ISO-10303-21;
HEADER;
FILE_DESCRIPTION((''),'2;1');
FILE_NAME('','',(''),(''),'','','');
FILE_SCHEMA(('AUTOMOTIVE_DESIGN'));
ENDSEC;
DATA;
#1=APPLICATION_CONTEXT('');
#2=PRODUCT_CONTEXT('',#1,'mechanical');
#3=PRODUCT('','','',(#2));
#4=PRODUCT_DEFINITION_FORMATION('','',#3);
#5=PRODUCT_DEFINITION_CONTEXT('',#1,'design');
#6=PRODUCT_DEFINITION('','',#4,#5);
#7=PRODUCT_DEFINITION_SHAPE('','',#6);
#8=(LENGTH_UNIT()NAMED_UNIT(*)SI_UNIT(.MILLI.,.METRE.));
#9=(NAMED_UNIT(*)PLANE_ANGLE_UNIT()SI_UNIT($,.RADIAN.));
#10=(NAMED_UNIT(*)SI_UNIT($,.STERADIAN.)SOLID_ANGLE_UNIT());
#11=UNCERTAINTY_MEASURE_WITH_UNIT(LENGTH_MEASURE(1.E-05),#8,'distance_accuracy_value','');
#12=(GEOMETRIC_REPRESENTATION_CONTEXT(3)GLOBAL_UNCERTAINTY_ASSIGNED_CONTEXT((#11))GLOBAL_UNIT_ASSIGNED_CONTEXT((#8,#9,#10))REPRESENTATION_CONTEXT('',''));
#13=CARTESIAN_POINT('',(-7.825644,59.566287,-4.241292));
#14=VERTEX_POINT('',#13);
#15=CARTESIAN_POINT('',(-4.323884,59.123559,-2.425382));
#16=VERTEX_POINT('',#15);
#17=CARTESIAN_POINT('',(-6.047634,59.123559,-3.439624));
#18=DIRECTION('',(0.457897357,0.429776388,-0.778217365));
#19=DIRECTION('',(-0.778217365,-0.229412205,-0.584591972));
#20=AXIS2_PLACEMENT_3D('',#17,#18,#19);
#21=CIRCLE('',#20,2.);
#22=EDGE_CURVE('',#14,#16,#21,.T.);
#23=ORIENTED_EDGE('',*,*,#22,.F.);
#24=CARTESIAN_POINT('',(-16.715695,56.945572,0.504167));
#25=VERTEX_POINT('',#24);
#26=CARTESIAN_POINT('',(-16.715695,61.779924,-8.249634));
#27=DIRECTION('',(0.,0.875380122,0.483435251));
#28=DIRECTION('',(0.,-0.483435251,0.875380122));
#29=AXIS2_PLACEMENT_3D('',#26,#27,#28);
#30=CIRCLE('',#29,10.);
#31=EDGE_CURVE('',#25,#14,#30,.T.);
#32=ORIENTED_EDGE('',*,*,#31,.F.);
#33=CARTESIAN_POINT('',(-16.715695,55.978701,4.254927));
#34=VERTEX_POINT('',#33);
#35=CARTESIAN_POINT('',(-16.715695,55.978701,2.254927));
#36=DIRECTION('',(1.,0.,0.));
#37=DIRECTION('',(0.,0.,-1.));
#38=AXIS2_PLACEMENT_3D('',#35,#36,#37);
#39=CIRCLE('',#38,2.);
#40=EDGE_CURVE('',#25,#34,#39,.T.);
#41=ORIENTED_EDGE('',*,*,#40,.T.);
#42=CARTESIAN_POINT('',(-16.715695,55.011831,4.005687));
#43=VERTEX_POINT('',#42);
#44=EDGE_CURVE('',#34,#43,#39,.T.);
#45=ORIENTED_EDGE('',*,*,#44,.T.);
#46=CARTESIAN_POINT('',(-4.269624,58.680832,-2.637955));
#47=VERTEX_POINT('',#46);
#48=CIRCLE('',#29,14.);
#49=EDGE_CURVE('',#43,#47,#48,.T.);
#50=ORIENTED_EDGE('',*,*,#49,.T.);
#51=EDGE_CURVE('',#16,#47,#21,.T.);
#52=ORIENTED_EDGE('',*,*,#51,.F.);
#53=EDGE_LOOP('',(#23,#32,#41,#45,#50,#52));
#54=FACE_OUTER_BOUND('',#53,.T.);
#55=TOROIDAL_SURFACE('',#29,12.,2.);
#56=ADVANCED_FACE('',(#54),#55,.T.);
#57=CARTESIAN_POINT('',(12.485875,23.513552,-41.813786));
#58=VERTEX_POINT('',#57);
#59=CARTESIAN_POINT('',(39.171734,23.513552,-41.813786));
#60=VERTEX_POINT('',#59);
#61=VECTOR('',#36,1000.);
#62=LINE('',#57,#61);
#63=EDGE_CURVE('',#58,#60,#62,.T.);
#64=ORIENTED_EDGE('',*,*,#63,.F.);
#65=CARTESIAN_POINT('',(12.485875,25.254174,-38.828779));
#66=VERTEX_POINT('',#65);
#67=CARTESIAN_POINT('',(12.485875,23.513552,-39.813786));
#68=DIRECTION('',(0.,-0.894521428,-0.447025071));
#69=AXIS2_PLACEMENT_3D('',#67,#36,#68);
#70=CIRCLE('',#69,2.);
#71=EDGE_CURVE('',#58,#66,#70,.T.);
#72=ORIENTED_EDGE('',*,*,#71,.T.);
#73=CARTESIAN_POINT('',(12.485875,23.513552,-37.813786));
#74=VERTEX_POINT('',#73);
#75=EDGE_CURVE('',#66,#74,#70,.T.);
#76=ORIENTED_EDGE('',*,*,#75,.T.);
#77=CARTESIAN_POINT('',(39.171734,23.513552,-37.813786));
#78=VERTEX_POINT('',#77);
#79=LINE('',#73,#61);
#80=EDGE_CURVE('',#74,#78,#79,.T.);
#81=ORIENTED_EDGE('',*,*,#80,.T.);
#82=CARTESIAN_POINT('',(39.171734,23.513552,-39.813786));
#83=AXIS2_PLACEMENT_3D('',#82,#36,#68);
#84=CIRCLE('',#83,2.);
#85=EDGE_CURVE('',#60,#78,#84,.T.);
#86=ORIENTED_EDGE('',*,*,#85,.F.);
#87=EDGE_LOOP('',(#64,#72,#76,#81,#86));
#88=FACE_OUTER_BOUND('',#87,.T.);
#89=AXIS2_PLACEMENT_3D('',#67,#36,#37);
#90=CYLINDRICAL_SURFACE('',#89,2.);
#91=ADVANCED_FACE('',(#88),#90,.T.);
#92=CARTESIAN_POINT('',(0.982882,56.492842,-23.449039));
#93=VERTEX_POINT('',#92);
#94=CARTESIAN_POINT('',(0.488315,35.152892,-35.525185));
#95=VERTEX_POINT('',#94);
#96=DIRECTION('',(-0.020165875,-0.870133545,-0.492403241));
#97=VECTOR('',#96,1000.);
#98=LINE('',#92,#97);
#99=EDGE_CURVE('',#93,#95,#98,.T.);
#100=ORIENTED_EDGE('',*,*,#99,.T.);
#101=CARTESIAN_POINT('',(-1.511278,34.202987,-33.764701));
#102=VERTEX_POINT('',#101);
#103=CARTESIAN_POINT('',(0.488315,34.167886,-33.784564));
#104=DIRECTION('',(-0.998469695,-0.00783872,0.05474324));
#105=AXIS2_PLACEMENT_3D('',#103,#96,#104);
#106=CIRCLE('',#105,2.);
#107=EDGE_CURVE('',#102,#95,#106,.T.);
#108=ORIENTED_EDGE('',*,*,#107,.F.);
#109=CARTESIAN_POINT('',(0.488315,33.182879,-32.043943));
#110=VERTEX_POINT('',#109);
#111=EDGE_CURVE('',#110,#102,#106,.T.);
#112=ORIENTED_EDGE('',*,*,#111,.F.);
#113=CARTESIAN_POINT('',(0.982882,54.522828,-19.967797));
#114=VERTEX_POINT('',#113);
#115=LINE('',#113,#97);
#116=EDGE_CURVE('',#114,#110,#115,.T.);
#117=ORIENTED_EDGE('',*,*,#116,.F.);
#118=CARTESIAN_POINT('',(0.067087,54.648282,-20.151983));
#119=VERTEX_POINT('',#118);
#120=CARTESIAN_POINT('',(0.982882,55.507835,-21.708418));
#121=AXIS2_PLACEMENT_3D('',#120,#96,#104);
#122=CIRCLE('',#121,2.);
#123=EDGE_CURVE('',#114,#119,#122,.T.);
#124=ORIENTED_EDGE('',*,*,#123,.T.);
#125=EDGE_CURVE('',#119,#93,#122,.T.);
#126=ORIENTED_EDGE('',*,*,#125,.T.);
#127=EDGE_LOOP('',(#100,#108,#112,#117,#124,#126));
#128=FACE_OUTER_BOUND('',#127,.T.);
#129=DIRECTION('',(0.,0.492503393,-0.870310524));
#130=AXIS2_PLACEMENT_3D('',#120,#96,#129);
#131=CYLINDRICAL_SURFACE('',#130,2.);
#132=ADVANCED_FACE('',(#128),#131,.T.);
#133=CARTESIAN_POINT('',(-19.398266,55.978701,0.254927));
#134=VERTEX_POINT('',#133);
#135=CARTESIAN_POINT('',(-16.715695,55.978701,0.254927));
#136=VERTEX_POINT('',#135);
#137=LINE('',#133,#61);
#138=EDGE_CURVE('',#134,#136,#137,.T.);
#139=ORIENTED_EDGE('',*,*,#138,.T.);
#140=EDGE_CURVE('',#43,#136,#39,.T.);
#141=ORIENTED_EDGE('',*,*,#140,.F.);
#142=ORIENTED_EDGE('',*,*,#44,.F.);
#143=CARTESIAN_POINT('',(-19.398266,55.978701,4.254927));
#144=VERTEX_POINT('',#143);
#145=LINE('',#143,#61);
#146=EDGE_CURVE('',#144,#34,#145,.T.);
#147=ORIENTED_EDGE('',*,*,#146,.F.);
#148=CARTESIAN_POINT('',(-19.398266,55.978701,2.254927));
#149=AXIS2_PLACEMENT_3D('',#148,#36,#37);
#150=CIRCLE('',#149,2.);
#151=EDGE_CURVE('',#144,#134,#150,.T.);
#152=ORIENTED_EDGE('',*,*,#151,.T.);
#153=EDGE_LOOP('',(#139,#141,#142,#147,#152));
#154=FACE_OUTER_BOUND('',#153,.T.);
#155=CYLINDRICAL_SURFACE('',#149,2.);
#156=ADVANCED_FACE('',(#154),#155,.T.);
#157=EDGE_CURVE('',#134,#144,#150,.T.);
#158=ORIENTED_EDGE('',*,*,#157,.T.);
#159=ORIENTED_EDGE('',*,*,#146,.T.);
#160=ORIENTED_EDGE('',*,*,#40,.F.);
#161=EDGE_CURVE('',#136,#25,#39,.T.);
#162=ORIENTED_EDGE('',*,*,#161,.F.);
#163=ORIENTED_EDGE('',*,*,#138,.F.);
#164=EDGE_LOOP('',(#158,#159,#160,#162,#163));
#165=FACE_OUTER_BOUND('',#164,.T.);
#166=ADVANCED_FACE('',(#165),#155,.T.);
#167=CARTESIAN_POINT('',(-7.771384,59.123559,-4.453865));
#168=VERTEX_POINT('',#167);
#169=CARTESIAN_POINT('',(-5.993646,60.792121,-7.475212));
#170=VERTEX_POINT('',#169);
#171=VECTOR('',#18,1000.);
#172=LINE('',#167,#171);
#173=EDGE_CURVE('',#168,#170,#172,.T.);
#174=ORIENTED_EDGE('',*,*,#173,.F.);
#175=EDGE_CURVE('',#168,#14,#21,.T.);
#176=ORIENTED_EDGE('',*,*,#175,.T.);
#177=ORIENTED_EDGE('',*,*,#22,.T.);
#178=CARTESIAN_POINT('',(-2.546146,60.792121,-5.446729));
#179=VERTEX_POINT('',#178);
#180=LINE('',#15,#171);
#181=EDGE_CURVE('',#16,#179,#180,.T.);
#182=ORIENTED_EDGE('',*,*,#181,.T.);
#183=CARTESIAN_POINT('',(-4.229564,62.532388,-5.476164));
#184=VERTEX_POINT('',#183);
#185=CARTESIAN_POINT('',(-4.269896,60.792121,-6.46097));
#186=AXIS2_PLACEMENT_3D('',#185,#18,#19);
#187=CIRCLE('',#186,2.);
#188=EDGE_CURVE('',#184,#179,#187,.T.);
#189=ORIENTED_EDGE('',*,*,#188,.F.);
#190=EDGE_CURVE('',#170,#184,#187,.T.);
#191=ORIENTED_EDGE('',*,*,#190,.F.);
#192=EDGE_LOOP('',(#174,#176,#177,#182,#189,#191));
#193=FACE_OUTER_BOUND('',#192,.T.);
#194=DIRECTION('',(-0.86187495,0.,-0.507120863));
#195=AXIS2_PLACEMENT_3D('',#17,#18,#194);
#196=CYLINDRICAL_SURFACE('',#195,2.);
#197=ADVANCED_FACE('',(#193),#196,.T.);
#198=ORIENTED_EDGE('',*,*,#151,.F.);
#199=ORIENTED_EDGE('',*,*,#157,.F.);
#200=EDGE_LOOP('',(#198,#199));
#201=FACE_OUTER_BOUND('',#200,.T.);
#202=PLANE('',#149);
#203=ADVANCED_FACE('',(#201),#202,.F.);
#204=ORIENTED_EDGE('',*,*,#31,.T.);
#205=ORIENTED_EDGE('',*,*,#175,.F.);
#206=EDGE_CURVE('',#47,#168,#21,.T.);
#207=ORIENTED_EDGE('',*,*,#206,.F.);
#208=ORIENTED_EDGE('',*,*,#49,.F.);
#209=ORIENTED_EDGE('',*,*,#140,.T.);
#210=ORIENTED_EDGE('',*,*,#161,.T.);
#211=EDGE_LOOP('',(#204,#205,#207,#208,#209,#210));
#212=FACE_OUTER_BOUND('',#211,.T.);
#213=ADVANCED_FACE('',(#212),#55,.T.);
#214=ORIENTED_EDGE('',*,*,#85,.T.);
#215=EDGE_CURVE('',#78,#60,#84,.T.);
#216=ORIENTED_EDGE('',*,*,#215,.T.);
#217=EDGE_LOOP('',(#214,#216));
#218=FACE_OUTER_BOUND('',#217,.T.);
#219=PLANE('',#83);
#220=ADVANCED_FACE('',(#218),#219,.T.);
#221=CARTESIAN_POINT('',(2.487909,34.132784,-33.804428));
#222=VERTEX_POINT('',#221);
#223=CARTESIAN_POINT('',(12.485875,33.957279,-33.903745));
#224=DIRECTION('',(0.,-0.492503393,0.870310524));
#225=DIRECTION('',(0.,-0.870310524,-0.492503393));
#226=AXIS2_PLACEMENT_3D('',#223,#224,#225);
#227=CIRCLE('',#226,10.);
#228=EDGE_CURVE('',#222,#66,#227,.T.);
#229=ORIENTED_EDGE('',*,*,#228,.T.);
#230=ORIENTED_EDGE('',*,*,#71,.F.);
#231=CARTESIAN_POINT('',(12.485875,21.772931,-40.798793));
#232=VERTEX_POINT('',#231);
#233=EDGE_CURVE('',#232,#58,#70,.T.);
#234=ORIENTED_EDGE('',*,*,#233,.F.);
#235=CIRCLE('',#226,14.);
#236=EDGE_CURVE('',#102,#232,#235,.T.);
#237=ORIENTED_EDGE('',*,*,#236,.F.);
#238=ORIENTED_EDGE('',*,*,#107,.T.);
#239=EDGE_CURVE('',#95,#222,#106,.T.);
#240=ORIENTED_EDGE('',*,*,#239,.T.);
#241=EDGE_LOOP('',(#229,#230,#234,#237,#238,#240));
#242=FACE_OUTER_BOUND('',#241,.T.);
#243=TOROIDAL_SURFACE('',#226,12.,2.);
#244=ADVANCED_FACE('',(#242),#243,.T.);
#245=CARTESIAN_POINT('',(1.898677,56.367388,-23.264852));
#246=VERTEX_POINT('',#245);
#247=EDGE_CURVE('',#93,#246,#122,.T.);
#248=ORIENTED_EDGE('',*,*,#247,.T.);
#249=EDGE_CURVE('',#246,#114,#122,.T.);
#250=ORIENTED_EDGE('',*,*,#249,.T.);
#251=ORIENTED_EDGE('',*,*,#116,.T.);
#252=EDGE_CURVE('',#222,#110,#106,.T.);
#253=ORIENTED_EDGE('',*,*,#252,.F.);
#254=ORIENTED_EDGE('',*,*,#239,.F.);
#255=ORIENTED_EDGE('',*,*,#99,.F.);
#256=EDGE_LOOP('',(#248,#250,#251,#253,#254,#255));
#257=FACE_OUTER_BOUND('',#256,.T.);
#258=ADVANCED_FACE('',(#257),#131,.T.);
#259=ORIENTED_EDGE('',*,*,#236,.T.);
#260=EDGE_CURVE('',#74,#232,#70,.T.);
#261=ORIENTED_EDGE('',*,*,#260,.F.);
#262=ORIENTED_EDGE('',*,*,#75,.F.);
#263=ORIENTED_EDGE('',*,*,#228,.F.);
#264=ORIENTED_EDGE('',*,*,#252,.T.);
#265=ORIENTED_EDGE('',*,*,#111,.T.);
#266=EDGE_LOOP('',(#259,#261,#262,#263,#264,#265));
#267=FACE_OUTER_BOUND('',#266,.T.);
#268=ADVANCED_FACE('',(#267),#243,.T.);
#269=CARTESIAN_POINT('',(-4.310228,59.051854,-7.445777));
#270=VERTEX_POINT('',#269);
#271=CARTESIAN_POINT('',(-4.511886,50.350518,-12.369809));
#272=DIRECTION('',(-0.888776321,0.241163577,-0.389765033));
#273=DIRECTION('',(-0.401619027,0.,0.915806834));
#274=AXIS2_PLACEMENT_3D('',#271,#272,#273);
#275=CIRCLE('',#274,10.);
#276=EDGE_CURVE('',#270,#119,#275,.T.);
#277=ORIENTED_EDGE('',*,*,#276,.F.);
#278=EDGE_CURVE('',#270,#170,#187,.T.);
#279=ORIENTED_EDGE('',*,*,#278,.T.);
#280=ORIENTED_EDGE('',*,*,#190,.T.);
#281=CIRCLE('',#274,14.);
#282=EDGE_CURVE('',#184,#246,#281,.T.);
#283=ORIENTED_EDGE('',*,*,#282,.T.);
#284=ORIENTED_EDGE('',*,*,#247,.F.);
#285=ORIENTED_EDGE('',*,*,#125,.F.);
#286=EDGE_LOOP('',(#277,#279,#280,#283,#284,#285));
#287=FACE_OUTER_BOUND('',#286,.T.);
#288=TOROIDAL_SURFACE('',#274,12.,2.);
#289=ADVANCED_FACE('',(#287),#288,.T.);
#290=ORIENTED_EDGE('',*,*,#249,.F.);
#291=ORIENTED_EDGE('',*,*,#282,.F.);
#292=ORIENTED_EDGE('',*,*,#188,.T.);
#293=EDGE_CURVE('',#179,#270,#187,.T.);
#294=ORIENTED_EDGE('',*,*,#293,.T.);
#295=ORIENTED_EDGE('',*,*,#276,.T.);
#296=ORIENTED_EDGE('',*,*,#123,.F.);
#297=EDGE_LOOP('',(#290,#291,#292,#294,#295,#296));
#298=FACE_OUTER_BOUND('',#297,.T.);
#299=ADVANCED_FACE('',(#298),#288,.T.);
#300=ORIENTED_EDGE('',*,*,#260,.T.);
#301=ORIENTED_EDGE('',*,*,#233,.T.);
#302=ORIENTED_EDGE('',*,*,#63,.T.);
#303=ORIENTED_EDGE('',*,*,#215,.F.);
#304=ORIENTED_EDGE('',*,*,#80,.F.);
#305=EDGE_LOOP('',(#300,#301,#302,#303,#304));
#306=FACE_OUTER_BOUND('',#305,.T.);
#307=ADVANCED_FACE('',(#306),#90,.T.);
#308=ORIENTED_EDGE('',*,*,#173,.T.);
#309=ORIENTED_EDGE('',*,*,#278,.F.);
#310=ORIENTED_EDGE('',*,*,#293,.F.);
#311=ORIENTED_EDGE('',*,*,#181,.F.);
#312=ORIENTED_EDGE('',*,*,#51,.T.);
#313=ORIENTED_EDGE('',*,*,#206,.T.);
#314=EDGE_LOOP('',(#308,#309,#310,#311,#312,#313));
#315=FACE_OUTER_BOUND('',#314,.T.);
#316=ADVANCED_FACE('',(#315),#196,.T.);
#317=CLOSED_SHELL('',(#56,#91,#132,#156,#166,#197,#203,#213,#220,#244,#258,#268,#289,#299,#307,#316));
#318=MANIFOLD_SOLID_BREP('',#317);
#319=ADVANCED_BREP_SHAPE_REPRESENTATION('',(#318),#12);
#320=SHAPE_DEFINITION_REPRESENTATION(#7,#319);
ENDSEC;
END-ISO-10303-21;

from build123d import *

# Parameters (mm, degrees)
SKETCH2_R = 2


with BuildPart() as part:
    # Sweep1: sweep along a curve in space
    with BuildLine() as sweep1_path:
        Line((-19.39826571, 55.978701071, 2.254926967), (-16.715694993, 55.978701071, 2.254926967))
        ThreePointArc((-6.047634181, 59.123559398, -3.439623567), (-10.468184265, 56.826927396, 0.719001604), (-16.715694993, 55.978701071, 2.254926967))
        Line((-6.047634181, 59.123559398, -3.439623567), (-4.269895959, 60.792120921, -6.460970453))
        ThreePointArc((0.98288182, 55.507835041, -21.708417726), (-0.455385422, 61.380619924, -14.795022607), (-4.269895959, 60.792120921, -6.460970453))
        Line((0.98288182, 55.507835041, -21.708417726), (0.488315483, 34.167885645, -33.784564331))
        ThreePointArc((12.48587526, 23.513552475, -39.813786189), (3.915464358, 26.647289087, -38.040423843), (0.488315483, 34.167885645, -33.784564331))
        Line((12.48587526, 23.513552475, -39.813786189), (39.17173429, 23.513552475, -39.813786189))
    # Sketch2 → Sweep1 (sweep)
    with BuildSketch(Plane(origin=(-19.39826571, 0, 0), x_dir=(0, 0, -1), z_dir=(1, 0, 0))):
        with Locations((-2.254926967, 55.978701071)):
            Circle(SKETCH2_R)
    sweep(path=sweep1_path.line)


solid = part.part
